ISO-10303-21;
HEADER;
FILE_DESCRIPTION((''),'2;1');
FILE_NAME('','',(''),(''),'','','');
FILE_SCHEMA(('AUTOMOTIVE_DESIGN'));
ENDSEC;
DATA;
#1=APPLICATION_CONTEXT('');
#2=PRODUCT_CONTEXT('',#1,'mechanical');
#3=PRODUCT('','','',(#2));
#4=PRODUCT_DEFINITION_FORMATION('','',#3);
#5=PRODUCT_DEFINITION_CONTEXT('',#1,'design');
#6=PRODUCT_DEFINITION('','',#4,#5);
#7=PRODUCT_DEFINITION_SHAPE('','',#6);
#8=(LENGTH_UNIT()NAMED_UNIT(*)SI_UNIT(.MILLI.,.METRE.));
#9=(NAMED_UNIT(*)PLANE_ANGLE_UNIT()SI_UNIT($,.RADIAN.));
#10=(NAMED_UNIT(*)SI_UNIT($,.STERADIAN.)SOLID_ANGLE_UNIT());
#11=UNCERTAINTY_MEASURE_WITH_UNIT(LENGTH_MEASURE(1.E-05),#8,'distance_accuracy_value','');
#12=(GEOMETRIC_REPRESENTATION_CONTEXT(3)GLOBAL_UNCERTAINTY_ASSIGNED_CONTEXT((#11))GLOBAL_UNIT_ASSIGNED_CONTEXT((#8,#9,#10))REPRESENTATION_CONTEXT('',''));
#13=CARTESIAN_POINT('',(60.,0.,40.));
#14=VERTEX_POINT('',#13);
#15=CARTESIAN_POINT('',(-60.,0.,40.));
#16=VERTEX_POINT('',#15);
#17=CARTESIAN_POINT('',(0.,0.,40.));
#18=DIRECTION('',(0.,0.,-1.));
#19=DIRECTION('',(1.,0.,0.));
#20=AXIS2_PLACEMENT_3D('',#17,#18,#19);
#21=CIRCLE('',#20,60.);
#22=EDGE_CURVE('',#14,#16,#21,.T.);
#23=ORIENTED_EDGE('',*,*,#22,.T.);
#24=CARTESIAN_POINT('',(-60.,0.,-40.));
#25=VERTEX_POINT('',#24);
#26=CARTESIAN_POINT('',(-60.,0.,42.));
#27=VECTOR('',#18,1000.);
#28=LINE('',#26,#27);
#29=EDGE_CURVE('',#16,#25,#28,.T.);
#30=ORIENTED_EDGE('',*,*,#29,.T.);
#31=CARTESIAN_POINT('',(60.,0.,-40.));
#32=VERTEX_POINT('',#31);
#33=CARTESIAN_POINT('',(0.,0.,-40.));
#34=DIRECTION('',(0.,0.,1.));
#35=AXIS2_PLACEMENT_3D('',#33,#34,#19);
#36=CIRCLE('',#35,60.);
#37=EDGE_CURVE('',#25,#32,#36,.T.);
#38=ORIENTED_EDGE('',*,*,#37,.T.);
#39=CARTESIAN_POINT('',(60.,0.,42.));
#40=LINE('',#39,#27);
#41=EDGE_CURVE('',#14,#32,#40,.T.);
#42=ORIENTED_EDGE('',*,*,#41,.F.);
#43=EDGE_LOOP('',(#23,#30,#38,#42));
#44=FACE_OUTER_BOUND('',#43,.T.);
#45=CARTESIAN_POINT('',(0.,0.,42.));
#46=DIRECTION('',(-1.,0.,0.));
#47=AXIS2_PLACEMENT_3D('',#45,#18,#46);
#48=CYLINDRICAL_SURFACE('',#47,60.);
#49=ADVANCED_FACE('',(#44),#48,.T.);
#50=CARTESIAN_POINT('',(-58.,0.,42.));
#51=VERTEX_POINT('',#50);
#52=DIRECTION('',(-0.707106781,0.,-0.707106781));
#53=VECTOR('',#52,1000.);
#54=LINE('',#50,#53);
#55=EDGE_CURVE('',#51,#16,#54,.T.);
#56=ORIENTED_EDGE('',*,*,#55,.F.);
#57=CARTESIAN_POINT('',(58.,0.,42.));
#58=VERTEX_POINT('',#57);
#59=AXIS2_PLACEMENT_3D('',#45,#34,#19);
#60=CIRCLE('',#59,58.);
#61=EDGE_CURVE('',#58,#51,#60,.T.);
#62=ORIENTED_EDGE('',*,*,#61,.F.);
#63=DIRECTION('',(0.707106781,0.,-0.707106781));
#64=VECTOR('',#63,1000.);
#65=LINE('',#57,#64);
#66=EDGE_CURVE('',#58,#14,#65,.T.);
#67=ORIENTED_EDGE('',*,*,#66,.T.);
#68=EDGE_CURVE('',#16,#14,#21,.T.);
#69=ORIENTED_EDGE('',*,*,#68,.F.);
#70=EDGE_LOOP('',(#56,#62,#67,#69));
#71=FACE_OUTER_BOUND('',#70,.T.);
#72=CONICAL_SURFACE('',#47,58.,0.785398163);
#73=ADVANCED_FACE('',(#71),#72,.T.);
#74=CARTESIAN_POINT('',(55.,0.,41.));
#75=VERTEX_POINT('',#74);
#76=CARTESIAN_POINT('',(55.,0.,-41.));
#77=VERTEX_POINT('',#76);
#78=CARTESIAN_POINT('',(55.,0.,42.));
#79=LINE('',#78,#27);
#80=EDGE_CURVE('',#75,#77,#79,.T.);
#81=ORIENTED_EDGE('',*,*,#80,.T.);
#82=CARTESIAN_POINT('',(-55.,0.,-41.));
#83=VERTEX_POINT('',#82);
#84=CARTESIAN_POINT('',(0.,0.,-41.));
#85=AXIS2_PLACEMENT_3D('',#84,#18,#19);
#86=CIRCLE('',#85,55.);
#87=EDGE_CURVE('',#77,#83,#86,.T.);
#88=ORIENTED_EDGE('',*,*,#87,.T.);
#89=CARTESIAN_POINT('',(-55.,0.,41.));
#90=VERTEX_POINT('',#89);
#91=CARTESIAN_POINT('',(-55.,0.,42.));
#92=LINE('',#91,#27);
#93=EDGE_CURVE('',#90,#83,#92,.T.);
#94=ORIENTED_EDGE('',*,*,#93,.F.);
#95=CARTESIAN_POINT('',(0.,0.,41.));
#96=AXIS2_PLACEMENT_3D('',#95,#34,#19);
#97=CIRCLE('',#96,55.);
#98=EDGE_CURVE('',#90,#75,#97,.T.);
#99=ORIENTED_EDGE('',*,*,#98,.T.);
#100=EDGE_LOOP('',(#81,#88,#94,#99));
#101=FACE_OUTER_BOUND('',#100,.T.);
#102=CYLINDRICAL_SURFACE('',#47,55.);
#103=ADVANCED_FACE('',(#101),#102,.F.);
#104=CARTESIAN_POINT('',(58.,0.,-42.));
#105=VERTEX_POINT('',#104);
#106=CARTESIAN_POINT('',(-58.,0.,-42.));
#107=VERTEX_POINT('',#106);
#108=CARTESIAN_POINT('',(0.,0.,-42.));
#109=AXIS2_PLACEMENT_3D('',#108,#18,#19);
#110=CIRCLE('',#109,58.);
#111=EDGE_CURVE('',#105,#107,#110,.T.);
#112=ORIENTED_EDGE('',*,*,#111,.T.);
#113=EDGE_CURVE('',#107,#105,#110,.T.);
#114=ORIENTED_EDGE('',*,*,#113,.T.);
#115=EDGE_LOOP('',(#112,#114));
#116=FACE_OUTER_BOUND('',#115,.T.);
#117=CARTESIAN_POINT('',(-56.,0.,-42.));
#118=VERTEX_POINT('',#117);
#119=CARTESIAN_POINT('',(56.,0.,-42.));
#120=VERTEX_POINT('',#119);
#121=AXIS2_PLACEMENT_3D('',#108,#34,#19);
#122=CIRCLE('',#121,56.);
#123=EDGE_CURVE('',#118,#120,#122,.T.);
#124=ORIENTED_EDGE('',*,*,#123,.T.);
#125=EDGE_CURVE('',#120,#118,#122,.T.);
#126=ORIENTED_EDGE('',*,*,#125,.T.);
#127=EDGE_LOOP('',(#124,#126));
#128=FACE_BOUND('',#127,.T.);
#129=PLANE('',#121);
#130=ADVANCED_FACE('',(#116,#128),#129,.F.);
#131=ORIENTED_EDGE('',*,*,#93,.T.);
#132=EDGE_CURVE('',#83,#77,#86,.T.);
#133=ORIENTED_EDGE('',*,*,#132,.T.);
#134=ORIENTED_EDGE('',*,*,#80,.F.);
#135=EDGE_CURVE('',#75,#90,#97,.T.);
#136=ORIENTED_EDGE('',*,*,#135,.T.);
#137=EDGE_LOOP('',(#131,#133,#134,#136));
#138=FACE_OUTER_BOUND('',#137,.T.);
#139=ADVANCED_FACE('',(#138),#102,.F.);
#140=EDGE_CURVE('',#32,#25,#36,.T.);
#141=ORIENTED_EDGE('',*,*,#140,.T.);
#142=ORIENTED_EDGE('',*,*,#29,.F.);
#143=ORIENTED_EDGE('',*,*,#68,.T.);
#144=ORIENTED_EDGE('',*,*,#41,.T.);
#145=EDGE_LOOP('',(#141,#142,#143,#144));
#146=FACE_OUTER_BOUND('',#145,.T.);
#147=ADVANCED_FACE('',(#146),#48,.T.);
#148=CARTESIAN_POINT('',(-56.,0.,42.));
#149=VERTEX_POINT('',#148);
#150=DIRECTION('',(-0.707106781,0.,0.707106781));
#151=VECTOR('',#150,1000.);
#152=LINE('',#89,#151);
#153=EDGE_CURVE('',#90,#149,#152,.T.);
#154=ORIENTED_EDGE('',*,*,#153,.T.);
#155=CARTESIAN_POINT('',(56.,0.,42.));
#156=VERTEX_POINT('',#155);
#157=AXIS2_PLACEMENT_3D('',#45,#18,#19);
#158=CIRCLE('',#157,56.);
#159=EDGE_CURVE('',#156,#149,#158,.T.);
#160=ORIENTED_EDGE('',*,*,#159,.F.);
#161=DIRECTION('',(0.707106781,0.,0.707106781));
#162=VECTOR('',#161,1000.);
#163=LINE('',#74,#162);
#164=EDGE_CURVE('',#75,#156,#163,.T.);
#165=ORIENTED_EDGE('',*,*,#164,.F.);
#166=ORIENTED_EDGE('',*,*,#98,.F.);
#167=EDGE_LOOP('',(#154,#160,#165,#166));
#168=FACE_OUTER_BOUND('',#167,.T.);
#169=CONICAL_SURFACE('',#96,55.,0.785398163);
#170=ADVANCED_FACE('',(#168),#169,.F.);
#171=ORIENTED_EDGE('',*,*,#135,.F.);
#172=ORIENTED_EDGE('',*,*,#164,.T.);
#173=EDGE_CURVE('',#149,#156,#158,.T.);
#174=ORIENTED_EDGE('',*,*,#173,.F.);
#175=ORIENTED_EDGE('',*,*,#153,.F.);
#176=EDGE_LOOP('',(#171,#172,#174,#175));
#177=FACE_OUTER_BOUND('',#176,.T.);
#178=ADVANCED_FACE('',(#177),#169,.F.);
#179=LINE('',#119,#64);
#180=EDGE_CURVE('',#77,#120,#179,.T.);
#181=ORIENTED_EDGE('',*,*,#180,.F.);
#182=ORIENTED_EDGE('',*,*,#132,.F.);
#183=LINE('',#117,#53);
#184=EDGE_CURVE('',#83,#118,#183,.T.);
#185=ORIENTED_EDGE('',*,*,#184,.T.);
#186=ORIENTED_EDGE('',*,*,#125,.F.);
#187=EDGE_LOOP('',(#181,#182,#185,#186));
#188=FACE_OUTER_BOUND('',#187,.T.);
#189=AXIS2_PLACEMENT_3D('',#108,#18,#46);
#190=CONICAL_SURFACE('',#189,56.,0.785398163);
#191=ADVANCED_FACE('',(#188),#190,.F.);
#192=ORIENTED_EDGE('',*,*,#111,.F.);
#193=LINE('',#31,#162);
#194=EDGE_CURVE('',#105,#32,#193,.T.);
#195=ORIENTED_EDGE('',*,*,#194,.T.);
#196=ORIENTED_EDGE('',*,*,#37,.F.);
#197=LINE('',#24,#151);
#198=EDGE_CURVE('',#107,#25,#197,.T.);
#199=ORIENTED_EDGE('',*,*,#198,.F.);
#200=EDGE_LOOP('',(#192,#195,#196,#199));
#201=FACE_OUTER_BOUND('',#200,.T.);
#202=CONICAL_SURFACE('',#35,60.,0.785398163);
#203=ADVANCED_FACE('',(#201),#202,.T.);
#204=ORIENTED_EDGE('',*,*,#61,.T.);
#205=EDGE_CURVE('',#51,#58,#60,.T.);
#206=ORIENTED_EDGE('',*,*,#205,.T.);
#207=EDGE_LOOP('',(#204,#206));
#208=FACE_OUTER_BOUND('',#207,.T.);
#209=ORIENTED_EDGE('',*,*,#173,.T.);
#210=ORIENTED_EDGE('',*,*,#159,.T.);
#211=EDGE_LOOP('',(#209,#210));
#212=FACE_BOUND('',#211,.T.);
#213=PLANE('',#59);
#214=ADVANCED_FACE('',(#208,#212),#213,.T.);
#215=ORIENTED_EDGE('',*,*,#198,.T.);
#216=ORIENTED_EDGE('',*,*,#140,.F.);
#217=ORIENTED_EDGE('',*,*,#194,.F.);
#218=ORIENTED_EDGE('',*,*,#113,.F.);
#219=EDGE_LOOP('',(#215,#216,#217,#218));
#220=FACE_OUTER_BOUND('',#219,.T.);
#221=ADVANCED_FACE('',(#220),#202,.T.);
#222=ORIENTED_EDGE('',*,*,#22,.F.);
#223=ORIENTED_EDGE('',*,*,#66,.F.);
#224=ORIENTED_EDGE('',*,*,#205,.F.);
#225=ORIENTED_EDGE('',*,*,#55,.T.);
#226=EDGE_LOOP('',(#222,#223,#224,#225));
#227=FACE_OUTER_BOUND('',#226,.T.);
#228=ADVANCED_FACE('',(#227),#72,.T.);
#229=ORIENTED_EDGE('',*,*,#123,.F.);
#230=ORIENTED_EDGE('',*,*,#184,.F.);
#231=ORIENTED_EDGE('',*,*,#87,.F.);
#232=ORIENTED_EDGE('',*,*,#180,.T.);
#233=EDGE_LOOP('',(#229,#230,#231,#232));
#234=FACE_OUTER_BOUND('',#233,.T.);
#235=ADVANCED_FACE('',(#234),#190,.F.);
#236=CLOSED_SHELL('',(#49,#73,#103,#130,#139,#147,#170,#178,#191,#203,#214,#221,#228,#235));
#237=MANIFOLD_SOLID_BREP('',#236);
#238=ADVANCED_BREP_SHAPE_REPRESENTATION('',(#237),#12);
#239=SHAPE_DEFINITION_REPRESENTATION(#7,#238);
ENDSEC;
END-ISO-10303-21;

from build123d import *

# Parameters (mm, degrees)
SKETCH1_R           = 60
SKETCH1_R_2         = 55
BOSS_EXTRUDE1_DEPTH = 42
CHAMFER1_SIZE       = 2
CHAMFER2_SIZE       = 1


with BuildPart() as part:
    # Sketch1 → Boss-Extrude1 (new, symmetric)
    with BuildSketch(Plane.XY):
        with Locations(Location((0, 0, 0), (0, 0, 180))):
            Circle(SKETCH1_R)
        with Locations(Location((0, 0, 0), (0, 0, 180))):
            Circle(SKETCH1_R_2, mode=Mode.SUBTRACT)
    extrude(amount=BOSS_EXTRUDE1_DEPTH, both=True)

    # Chamfer1
    chamfer1_edges = [part.edges().sort_by_distance(p)[0] for p in [
        (60, 0, -42),
        (60, 0, 42),
    ]]
    chamfer(chamfer1_edges, length=CHAMFER1_SIZE)

    # Chamfer2
    chamfer2_edges = [part.edges().sort_by_distance(p)[0] for p in [
        (55, 0, -42),
        (55, 0, 42),
    ]]
    chamfer(chamfer2_edges, length=CHAMFER2_SIZE)


solid = part.part
